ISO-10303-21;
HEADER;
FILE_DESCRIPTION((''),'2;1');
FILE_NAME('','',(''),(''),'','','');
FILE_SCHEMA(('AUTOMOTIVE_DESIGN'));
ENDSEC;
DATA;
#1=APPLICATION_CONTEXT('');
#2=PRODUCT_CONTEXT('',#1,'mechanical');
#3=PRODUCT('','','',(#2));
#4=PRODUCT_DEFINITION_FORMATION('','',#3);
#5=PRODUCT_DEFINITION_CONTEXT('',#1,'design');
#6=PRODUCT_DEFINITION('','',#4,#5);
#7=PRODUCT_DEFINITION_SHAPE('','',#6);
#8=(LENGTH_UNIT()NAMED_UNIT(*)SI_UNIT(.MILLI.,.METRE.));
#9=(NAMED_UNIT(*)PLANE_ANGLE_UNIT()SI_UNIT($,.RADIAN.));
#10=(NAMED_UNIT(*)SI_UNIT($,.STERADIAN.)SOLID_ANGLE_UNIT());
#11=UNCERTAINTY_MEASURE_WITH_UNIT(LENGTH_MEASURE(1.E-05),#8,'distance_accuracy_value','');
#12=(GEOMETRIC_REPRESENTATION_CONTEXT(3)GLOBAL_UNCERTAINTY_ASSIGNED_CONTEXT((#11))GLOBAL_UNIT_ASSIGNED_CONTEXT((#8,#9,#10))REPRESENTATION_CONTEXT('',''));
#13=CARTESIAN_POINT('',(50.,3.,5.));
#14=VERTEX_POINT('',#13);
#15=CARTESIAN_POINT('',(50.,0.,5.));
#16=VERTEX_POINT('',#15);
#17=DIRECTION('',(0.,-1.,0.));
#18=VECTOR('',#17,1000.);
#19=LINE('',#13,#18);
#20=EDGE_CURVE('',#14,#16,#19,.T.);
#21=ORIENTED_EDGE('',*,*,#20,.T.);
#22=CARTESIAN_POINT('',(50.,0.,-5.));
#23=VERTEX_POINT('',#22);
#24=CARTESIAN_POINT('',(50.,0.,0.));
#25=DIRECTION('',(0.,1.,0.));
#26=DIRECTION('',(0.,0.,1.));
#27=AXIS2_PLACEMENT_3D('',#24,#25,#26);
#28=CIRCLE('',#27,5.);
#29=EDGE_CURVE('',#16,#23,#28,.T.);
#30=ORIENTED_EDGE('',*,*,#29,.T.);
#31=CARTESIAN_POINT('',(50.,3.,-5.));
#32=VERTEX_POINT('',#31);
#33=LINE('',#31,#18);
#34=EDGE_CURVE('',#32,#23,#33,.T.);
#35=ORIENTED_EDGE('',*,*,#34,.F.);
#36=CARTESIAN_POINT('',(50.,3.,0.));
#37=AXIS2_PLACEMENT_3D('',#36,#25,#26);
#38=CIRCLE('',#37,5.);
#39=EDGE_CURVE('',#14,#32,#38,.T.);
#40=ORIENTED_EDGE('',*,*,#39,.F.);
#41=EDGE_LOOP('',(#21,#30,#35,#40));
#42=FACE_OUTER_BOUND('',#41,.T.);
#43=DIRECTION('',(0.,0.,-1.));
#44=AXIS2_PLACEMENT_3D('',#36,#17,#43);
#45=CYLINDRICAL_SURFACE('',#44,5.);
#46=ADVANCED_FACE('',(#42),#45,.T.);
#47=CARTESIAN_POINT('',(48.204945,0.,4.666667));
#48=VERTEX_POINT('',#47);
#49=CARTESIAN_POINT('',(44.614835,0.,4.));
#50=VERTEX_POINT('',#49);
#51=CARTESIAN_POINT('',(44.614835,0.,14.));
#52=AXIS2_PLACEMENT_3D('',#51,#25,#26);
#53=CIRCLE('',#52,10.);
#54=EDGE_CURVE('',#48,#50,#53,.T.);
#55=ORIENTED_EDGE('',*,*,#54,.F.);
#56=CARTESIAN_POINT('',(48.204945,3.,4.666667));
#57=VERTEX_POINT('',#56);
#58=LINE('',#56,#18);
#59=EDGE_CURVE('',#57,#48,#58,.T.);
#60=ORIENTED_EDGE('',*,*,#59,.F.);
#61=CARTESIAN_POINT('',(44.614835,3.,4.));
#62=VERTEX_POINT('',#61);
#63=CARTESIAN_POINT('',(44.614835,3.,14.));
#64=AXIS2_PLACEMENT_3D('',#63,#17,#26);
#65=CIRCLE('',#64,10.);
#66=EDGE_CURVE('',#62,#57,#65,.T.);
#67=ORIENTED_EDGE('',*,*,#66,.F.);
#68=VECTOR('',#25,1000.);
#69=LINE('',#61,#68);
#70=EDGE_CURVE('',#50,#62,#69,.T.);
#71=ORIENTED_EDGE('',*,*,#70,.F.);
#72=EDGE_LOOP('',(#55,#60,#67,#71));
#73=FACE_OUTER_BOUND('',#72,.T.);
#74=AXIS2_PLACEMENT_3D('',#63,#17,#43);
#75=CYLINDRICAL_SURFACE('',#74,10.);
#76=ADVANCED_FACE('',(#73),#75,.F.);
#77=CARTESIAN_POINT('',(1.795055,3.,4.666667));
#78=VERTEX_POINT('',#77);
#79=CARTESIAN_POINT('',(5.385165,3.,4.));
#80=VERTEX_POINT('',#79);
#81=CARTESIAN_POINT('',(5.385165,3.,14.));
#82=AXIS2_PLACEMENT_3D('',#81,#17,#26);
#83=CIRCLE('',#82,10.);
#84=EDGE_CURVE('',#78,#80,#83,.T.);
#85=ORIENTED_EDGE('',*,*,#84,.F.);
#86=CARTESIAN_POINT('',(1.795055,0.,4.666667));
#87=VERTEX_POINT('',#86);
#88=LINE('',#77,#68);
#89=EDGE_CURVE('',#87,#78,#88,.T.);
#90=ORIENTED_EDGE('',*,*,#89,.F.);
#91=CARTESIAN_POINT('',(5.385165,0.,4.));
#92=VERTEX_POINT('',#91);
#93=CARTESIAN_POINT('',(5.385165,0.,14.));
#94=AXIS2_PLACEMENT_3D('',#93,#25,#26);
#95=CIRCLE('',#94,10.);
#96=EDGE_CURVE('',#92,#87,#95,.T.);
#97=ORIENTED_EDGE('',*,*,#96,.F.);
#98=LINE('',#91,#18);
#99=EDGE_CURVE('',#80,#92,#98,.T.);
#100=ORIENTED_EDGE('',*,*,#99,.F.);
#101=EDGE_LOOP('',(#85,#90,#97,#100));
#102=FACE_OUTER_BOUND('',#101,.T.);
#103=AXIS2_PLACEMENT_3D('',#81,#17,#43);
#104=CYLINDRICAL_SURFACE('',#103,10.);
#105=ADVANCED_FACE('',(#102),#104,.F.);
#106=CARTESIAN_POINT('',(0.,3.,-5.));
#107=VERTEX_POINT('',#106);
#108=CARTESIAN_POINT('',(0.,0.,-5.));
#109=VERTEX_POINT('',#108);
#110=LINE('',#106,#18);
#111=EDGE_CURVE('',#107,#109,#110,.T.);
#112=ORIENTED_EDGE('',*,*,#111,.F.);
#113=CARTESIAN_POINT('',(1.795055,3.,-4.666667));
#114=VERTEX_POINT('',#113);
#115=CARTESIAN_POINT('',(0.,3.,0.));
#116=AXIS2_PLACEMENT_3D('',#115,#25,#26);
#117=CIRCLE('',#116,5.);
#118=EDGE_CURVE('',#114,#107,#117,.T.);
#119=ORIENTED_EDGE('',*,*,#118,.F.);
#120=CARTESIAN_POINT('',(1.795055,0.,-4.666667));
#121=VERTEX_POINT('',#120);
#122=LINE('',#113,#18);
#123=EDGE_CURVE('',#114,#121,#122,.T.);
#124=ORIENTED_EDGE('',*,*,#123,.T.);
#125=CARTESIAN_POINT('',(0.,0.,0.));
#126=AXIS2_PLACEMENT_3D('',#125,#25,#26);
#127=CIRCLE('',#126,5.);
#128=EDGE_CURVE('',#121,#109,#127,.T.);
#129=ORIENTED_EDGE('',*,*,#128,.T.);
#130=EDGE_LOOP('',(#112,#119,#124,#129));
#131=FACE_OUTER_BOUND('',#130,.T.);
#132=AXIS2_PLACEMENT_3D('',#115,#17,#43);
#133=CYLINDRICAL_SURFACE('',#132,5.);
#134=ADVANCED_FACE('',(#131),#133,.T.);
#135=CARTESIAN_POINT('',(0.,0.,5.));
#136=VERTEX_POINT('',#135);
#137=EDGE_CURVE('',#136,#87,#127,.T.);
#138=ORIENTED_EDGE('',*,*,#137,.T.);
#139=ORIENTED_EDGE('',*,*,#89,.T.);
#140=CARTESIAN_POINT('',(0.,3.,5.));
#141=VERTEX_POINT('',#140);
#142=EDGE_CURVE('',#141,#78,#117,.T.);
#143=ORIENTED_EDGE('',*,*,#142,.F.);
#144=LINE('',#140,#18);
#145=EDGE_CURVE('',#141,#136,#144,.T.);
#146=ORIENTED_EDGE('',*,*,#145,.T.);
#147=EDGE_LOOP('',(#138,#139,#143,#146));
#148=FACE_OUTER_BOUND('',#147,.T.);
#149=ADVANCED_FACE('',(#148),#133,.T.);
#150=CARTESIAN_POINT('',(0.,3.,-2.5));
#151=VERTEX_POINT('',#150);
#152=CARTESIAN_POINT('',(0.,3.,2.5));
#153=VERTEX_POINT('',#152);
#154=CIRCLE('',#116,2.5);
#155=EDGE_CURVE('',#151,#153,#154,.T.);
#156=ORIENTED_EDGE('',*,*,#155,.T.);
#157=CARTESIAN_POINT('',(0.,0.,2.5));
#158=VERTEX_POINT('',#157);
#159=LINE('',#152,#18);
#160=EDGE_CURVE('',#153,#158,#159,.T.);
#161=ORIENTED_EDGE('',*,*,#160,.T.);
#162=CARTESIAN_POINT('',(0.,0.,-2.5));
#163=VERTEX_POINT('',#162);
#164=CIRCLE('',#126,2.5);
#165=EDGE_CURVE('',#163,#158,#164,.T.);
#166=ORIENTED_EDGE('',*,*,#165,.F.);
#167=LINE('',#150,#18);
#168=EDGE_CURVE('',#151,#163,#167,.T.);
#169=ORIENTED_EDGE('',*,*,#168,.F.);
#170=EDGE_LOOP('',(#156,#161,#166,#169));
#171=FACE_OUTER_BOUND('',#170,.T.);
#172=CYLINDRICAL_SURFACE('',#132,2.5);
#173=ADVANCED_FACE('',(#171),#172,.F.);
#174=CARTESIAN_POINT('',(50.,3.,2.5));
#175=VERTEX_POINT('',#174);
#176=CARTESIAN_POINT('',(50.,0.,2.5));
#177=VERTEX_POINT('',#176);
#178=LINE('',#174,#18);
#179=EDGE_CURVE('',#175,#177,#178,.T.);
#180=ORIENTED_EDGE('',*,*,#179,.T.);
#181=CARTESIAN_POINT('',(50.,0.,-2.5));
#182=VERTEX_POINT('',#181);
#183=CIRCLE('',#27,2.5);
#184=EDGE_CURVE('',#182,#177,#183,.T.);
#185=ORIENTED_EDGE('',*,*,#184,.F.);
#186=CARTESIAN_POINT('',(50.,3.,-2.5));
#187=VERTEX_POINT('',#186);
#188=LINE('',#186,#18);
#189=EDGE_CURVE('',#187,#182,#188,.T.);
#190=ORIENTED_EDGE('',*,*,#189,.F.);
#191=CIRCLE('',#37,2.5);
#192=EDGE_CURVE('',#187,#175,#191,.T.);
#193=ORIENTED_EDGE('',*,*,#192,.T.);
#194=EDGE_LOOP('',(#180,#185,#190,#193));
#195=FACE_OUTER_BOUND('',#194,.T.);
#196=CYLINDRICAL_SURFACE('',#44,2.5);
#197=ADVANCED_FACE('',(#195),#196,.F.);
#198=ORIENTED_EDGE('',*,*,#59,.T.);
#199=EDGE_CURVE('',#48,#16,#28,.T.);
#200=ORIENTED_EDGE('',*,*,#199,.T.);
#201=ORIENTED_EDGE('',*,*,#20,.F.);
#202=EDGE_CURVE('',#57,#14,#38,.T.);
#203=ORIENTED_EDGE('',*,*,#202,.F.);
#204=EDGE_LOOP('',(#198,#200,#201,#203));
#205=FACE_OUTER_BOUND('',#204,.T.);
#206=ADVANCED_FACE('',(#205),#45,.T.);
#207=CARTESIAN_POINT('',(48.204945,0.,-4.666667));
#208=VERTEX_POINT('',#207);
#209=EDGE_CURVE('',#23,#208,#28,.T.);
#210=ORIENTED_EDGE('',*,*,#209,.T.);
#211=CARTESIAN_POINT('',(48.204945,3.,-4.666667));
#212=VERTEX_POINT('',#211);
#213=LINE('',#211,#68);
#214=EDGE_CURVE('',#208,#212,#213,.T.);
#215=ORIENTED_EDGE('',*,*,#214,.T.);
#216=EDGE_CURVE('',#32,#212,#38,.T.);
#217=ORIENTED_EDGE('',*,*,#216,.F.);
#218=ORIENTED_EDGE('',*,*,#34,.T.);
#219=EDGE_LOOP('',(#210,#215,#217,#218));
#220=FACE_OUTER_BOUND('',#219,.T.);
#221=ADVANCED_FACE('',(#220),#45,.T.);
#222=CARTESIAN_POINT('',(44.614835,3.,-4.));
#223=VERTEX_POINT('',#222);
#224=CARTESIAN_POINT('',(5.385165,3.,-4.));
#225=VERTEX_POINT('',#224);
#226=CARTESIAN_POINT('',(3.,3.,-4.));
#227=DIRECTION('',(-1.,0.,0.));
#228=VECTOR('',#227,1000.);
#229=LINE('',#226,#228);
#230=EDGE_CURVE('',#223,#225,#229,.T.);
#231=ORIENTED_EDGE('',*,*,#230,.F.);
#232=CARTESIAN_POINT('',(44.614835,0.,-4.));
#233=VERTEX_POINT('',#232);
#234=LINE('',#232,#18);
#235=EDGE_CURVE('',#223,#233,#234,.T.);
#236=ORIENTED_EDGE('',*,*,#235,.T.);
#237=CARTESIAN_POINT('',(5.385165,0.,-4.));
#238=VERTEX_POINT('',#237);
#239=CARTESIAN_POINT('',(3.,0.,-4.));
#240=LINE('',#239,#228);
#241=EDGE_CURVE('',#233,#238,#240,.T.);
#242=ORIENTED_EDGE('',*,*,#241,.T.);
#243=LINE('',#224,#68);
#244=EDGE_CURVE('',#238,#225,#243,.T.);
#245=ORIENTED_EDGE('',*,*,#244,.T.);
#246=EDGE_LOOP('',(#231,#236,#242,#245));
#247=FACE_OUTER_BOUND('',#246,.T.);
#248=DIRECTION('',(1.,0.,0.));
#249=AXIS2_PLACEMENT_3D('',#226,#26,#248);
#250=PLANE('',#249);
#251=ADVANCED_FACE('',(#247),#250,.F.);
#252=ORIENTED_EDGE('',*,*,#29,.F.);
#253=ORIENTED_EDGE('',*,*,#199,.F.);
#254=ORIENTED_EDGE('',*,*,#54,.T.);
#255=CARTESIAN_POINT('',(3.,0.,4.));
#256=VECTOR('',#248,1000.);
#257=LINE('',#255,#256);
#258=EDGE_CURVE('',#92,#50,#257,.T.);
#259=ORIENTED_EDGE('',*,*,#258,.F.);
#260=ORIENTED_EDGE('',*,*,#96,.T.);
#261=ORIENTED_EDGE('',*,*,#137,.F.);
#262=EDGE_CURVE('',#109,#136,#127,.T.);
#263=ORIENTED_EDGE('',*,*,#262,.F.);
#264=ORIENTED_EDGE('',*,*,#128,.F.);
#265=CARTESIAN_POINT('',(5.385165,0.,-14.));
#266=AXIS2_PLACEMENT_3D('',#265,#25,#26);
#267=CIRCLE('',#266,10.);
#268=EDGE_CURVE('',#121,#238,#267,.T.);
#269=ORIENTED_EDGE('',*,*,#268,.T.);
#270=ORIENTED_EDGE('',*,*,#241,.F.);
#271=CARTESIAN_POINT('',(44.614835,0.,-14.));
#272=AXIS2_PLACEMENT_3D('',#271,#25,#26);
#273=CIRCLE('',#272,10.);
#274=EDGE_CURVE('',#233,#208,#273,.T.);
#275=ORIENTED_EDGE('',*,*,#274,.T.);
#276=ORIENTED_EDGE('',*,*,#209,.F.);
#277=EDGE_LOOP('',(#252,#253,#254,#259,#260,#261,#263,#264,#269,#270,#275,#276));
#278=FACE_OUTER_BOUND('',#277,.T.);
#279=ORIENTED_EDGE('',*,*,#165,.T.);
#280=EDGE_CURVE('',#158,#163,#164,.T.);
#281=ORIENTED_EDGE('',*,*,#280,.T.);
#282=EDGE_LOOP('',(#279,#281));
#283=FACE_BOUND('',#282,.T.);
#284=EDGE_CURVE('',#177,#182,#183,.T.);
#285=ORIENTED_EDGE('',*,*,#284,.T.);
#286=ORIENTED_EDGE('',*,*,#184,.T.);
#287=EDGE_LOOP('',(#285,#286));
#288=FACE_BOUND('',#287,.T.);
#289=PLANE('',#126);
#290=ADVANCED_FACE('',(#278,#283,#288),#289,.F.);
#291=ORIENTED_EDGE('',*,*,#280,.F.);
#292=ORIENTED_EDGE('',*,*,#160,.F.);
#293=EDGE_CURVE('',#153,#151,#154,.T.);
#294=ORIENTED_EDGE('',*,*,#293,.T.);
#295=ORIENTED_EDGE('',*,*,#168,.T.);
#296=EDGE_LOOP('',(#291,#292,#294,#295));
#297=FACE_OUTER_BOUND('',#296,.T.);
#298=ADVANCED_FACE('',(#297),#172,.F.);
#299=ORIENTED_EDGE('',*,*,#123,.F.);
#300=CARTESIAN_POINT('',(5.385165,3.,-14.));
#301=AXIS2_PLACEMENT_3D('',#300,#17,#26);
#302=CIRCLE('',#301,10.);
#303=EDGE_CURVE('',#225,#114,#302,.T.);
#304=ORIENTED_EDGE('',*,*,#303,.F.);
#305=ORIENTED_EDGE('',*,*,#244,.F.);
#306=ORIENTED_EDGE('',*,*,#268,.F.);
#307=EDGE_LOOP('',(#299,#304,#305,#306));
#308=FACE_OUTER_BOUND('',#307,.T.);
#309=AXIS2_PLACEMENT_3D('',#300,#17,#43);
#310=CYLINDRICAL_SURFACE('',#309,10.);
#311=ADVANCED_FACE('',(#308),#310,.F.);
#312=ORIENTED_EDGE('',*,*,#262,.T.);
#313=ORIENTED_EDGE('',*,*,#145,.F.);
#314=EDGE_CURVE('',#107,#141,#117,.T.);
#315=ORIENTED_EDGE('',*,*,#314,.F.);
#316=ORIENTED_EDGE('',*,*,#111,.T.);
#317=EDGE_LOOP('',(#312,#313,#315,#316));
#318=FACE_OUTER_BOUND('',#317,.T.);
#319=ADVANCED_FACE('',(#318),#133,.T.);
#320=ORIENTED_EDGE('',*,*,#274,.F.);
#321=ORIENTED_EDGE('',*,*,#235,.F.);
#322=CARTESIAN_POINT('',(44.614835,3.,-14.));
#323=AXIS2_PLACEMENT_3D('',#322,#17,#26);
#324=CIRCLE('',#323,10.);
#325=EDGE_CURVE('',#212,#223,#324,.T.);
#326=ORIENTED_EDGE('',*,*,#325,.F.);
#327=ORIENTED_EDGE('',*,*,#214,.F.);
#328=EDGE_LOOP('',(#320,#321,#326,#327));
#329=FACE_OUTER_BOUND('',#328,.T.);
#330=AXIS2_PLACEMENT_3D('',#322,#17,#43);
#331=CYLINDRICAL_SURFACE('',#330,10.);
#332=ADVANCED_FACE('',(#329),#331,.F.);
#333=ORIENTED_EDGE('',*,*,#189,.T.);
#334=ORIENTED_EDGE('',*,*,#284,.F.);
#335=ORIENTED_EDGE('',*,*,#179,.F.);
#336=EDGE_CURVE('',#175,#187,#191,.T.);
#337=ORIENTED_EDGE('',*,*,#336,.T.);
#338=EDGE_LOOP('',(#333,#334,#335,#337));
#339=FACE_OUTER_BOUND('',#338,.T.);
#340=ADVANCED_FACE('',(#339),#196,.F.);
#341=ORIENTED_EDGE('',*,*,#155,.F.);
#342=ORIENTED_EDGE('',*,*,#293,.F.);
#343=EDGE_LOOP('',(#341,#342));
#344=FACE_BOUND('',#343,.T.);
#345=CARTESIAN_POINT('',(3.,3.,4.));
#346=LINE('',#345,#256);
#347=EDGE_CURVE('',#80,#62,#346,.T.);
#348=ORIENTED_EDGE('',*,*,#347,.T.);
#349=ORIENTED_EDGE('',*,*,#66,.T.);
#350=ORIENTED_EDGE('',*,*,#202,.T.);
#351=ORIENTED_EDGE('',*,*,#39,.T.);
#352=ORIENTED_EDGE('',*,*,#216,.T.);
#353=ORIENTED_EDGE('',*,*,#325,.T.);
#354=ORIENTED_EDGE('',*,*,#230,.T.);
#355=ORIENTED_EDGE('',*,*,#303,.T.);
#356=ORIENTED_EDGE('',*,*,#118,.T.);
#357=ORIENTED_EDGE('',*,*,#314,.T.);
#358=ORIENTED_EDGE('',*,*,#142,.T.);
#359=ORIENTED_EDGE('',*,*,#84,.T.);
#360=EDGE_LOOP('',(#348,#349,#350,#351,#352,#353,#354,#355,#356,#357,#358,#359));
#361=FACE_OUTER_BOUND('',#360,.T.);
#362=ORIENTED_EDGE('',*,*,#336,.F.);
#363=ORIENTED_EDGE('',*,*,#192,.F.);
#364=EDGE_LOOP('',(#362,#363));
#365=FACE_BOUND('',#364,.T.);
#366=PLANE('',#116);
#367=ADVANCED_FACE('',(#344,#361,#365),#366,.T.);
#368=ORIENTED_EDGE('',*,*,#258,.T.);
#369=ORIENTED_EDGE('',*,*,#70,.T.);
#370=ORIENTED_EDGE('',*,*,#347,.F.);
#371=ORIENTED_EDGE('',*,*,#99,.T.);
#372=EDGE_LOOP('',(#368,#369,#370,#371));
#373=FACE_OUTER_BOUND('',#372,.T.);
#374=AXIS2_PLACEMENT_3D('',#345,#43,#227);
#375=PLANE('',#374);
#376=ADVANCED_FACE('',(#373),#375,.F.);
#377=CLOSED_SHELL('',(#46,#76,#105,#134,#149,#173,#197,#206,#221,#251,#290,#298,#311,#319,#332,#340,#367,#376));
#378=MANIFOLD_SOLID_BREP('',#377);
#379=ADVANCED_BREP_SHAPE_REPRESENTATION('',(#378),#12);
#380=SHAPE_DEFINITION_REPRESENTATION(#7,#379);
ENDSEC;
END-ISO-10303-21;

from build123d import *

# Parameters (mm, degrees)
SKETCH_1_R      = 2.5
EXTRUDE_1_DEPTH = 3
FILLET_1_R      = 10


with BuildPart() as part:
    # 草图1 → 凸台-拉伸1 (new body)
    with BuildSketch(Plane(origin=(0, 0, 0), x_dir=(1, 0, 0), z_dir=(0, 1, 0))):
        with BuildLine():
            Line((3, -4), (47, -4))
            ThreePointArc((47, -4), (55, 0), (47, 4))
            Line((47, 4), (3, 4))
            ThreePointArc((3, 4), (-5, 0), (3, -4))
        make_face()
        with Locations(Location((0, 0, 0), (0, 0, 270))):
            Circle(SKETCH_1_R, mode=Mode.SUBTRACT)
        with Locations(Location((50, 0, 0), (0, 0, 270))):
            Circle(SKETCH_1_R, mode=Mode.SUBTRACT)
    extrude(amount=EXTRUDE_1_DEPTH)

    # 圆角1
    fillet_1_edges = [part.edges().sort_by_distance(p)[0] for p in [
        (3, 1.5, -4),
        (47, 1.5, -4),
        (47, 1.5, 4),
        (3, 1.5, 4),
    ]]
    fillet(fillet_1_edges, radius=FILLET_1_R)


solid = part.part
